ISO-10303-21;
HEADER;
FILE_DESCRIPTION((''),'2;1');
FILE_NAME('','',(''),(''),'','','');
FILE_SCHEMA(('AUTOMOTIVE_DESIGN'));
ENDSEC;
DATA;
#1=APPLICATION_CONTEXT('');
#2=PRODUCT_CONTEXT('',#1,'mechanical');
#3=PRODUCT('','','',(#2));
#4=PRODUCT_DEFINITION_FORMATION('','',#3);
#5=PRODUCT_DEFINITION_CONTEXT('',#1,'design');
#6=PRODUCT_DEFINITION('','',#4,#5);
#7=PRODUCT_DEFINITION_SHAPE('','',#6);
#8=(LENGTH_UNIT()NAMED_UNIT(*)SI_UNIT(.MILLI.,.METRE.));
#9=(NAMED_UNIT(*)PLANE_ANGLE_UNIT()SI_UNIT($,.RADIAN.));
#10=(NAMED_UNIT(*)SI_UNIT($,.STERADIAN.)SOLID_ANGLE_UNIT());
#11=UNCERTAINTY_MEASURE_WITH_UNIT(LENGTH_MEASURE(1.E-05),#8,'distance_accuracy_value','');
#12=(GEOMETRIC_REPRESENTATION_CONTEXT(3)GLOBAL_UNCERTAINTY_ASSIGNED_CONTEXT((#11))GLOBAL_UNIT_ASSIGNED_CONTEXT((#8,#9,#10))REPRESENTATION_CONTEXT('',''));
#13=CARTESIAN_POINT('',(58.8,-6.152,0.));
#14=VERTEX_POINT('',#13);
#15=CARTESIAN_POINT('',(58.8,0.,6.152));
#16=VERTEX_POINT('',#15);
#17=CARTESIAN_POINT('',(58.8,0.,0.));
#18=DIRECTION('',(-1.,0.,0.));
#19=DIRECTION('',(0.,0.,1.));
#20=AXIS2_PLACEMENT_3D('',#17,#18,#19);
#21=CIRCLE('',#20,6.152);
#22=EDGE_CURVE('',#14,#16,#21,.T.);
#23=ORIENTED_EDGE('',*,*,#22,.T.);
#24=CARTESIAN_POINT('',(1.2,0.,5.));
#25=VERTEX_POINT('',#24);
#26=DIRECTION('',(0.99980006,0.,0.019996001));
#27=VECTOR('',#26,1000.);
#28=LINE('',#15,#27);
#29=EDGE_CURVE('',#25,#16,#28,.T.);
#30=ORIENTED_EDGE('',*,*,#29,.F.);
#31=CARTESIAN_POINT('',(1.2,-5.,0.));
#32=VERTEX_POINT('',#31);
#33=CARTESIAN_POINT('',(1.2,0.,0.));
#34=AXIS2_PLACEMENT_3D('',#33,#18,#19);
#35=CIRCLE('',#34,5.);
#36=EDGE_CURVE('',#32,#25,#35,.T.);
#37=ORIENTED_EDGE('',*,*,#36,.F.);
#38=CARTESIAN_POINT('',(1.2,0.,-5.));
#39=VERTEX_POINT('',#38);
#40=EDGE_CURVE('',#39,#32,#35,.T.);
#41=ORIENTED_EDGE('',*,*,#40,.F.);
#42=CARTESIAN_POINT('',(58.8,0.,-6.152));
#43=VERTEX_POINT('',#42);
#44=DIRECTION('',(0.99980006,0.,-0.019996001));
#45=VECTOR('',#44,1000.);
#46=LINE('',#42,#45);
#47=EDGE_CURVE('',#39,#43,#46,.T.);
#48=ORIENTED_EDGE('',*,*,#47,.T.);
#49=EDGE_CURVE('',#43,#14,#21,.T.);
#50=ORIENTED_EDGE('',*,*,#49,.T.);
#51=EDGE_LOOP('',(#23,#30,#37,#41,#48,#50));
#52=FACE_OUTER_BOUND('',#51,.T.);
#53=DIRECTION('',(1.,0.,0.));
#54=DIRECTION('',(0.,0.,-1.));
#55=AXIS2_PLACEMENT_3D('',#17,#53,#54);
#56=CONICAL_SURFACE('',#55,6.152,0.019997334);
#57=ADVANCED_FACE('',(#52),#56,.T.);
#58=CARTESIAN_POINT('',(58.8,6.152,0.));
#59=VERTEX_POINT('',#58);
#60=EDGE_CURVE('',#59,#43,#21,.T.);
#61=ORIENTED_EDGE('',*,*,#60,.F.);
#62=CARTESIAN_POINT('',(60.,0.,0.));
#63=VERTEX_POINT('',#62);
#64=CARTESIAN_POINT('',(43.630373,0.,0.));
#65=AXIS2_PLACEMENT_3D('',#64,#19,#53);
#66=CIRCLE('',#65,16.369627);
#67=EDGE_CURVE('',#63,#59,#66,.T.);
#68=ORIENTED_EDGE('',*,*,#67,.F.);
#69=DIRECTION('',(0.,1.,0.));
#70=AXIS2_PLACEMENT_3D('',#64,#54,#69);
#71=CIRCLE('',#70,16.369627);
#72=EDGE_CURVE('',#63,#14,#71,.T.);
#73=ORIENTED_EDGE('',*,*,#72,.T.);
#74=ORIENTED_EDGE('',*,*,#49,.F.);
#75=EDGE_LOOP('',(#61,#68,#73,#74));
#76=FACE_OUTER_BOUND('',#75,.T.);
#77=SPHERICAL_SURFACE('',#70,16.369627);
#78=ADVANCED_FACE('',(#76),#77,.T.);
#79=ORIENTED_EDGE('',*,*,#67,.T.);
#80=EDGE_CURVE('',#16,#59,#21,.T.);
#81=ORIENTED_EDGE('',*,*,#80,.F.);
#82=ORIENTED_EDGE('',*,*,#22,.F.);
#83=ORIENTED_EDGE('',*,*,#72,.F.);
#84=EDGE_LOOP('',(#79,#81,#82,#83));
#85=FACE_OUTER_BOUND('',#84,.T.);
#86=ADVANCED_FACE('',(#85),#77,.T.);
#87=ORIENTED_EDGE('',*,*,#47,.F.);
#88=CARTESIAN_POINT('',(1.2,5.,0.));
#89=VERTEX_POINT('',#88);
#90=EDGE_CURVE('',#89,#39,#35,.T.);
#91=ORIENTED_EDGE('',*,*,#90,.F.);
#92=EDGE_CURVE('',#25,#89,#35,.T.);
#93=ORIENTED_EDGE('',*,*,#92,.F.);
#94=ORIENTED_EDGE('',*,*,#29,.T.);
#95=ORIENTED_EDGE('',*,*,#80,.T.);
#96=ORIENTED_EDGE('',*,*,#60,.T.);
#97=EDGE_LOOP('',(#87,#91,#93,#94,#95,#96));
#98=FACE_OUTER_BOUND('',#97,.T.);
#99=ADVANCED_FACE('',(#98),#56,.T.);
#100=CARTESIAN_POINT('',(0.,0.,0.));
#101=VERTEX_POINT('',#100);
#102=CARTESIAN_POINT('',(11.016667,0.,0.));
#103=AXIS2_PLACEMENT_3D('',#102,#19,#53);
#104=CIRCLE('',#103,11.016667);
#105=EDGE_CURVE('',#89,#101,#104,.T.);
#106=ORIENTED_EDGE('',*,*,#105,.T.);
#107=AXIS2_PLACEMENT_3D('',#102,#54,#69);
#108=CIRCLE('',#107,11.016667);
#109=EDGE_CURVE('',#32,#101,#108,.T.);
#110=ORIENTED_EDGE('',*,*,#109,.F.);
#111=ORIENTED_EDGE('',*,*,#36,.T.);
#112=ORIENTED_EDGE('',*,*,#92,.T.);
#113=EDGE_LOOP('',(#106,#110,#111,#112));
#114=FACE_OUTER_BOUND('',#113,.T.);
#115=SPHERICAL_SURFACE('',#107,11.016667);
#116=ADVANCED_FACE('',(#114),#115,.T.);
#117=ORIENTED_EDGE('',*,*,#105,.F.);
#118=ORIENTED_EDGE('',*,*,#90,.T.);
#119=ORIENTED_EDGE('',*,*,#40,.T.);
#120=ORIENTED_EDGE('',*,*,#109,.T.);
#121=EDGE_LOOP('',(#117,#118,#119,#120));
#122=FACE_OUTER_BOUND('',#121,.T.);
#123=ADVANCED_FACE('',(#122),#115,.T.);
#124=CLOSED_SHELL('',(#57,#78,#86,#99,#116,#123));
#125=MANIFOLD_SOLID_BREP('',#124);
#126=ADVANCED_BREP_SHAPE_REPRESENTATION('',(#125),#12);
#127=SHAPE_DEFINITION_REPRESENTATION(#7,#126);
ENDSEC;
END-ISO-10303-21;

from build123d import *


with BuildPart() as part:
    # Sketch1 → Base-Revolve (revolve)
    with BuildSketch(Plane.XY):
        with BuildLine():
            Line((0, 0), (60, 0))
            ThreePointArc((60, 0), (59.697199442, 3.133971283), (58.8, 6.152))
            Line((58.8, 6.152), (1.2, 5))
            ThreePointArc((1.2, 5), (0.30419989, 2.570992026), (0, 0))
        make_face()
    revolve(axis=Axis((-4.003548939, 0, 0), (1, 0, 0)))


solid = part.part
